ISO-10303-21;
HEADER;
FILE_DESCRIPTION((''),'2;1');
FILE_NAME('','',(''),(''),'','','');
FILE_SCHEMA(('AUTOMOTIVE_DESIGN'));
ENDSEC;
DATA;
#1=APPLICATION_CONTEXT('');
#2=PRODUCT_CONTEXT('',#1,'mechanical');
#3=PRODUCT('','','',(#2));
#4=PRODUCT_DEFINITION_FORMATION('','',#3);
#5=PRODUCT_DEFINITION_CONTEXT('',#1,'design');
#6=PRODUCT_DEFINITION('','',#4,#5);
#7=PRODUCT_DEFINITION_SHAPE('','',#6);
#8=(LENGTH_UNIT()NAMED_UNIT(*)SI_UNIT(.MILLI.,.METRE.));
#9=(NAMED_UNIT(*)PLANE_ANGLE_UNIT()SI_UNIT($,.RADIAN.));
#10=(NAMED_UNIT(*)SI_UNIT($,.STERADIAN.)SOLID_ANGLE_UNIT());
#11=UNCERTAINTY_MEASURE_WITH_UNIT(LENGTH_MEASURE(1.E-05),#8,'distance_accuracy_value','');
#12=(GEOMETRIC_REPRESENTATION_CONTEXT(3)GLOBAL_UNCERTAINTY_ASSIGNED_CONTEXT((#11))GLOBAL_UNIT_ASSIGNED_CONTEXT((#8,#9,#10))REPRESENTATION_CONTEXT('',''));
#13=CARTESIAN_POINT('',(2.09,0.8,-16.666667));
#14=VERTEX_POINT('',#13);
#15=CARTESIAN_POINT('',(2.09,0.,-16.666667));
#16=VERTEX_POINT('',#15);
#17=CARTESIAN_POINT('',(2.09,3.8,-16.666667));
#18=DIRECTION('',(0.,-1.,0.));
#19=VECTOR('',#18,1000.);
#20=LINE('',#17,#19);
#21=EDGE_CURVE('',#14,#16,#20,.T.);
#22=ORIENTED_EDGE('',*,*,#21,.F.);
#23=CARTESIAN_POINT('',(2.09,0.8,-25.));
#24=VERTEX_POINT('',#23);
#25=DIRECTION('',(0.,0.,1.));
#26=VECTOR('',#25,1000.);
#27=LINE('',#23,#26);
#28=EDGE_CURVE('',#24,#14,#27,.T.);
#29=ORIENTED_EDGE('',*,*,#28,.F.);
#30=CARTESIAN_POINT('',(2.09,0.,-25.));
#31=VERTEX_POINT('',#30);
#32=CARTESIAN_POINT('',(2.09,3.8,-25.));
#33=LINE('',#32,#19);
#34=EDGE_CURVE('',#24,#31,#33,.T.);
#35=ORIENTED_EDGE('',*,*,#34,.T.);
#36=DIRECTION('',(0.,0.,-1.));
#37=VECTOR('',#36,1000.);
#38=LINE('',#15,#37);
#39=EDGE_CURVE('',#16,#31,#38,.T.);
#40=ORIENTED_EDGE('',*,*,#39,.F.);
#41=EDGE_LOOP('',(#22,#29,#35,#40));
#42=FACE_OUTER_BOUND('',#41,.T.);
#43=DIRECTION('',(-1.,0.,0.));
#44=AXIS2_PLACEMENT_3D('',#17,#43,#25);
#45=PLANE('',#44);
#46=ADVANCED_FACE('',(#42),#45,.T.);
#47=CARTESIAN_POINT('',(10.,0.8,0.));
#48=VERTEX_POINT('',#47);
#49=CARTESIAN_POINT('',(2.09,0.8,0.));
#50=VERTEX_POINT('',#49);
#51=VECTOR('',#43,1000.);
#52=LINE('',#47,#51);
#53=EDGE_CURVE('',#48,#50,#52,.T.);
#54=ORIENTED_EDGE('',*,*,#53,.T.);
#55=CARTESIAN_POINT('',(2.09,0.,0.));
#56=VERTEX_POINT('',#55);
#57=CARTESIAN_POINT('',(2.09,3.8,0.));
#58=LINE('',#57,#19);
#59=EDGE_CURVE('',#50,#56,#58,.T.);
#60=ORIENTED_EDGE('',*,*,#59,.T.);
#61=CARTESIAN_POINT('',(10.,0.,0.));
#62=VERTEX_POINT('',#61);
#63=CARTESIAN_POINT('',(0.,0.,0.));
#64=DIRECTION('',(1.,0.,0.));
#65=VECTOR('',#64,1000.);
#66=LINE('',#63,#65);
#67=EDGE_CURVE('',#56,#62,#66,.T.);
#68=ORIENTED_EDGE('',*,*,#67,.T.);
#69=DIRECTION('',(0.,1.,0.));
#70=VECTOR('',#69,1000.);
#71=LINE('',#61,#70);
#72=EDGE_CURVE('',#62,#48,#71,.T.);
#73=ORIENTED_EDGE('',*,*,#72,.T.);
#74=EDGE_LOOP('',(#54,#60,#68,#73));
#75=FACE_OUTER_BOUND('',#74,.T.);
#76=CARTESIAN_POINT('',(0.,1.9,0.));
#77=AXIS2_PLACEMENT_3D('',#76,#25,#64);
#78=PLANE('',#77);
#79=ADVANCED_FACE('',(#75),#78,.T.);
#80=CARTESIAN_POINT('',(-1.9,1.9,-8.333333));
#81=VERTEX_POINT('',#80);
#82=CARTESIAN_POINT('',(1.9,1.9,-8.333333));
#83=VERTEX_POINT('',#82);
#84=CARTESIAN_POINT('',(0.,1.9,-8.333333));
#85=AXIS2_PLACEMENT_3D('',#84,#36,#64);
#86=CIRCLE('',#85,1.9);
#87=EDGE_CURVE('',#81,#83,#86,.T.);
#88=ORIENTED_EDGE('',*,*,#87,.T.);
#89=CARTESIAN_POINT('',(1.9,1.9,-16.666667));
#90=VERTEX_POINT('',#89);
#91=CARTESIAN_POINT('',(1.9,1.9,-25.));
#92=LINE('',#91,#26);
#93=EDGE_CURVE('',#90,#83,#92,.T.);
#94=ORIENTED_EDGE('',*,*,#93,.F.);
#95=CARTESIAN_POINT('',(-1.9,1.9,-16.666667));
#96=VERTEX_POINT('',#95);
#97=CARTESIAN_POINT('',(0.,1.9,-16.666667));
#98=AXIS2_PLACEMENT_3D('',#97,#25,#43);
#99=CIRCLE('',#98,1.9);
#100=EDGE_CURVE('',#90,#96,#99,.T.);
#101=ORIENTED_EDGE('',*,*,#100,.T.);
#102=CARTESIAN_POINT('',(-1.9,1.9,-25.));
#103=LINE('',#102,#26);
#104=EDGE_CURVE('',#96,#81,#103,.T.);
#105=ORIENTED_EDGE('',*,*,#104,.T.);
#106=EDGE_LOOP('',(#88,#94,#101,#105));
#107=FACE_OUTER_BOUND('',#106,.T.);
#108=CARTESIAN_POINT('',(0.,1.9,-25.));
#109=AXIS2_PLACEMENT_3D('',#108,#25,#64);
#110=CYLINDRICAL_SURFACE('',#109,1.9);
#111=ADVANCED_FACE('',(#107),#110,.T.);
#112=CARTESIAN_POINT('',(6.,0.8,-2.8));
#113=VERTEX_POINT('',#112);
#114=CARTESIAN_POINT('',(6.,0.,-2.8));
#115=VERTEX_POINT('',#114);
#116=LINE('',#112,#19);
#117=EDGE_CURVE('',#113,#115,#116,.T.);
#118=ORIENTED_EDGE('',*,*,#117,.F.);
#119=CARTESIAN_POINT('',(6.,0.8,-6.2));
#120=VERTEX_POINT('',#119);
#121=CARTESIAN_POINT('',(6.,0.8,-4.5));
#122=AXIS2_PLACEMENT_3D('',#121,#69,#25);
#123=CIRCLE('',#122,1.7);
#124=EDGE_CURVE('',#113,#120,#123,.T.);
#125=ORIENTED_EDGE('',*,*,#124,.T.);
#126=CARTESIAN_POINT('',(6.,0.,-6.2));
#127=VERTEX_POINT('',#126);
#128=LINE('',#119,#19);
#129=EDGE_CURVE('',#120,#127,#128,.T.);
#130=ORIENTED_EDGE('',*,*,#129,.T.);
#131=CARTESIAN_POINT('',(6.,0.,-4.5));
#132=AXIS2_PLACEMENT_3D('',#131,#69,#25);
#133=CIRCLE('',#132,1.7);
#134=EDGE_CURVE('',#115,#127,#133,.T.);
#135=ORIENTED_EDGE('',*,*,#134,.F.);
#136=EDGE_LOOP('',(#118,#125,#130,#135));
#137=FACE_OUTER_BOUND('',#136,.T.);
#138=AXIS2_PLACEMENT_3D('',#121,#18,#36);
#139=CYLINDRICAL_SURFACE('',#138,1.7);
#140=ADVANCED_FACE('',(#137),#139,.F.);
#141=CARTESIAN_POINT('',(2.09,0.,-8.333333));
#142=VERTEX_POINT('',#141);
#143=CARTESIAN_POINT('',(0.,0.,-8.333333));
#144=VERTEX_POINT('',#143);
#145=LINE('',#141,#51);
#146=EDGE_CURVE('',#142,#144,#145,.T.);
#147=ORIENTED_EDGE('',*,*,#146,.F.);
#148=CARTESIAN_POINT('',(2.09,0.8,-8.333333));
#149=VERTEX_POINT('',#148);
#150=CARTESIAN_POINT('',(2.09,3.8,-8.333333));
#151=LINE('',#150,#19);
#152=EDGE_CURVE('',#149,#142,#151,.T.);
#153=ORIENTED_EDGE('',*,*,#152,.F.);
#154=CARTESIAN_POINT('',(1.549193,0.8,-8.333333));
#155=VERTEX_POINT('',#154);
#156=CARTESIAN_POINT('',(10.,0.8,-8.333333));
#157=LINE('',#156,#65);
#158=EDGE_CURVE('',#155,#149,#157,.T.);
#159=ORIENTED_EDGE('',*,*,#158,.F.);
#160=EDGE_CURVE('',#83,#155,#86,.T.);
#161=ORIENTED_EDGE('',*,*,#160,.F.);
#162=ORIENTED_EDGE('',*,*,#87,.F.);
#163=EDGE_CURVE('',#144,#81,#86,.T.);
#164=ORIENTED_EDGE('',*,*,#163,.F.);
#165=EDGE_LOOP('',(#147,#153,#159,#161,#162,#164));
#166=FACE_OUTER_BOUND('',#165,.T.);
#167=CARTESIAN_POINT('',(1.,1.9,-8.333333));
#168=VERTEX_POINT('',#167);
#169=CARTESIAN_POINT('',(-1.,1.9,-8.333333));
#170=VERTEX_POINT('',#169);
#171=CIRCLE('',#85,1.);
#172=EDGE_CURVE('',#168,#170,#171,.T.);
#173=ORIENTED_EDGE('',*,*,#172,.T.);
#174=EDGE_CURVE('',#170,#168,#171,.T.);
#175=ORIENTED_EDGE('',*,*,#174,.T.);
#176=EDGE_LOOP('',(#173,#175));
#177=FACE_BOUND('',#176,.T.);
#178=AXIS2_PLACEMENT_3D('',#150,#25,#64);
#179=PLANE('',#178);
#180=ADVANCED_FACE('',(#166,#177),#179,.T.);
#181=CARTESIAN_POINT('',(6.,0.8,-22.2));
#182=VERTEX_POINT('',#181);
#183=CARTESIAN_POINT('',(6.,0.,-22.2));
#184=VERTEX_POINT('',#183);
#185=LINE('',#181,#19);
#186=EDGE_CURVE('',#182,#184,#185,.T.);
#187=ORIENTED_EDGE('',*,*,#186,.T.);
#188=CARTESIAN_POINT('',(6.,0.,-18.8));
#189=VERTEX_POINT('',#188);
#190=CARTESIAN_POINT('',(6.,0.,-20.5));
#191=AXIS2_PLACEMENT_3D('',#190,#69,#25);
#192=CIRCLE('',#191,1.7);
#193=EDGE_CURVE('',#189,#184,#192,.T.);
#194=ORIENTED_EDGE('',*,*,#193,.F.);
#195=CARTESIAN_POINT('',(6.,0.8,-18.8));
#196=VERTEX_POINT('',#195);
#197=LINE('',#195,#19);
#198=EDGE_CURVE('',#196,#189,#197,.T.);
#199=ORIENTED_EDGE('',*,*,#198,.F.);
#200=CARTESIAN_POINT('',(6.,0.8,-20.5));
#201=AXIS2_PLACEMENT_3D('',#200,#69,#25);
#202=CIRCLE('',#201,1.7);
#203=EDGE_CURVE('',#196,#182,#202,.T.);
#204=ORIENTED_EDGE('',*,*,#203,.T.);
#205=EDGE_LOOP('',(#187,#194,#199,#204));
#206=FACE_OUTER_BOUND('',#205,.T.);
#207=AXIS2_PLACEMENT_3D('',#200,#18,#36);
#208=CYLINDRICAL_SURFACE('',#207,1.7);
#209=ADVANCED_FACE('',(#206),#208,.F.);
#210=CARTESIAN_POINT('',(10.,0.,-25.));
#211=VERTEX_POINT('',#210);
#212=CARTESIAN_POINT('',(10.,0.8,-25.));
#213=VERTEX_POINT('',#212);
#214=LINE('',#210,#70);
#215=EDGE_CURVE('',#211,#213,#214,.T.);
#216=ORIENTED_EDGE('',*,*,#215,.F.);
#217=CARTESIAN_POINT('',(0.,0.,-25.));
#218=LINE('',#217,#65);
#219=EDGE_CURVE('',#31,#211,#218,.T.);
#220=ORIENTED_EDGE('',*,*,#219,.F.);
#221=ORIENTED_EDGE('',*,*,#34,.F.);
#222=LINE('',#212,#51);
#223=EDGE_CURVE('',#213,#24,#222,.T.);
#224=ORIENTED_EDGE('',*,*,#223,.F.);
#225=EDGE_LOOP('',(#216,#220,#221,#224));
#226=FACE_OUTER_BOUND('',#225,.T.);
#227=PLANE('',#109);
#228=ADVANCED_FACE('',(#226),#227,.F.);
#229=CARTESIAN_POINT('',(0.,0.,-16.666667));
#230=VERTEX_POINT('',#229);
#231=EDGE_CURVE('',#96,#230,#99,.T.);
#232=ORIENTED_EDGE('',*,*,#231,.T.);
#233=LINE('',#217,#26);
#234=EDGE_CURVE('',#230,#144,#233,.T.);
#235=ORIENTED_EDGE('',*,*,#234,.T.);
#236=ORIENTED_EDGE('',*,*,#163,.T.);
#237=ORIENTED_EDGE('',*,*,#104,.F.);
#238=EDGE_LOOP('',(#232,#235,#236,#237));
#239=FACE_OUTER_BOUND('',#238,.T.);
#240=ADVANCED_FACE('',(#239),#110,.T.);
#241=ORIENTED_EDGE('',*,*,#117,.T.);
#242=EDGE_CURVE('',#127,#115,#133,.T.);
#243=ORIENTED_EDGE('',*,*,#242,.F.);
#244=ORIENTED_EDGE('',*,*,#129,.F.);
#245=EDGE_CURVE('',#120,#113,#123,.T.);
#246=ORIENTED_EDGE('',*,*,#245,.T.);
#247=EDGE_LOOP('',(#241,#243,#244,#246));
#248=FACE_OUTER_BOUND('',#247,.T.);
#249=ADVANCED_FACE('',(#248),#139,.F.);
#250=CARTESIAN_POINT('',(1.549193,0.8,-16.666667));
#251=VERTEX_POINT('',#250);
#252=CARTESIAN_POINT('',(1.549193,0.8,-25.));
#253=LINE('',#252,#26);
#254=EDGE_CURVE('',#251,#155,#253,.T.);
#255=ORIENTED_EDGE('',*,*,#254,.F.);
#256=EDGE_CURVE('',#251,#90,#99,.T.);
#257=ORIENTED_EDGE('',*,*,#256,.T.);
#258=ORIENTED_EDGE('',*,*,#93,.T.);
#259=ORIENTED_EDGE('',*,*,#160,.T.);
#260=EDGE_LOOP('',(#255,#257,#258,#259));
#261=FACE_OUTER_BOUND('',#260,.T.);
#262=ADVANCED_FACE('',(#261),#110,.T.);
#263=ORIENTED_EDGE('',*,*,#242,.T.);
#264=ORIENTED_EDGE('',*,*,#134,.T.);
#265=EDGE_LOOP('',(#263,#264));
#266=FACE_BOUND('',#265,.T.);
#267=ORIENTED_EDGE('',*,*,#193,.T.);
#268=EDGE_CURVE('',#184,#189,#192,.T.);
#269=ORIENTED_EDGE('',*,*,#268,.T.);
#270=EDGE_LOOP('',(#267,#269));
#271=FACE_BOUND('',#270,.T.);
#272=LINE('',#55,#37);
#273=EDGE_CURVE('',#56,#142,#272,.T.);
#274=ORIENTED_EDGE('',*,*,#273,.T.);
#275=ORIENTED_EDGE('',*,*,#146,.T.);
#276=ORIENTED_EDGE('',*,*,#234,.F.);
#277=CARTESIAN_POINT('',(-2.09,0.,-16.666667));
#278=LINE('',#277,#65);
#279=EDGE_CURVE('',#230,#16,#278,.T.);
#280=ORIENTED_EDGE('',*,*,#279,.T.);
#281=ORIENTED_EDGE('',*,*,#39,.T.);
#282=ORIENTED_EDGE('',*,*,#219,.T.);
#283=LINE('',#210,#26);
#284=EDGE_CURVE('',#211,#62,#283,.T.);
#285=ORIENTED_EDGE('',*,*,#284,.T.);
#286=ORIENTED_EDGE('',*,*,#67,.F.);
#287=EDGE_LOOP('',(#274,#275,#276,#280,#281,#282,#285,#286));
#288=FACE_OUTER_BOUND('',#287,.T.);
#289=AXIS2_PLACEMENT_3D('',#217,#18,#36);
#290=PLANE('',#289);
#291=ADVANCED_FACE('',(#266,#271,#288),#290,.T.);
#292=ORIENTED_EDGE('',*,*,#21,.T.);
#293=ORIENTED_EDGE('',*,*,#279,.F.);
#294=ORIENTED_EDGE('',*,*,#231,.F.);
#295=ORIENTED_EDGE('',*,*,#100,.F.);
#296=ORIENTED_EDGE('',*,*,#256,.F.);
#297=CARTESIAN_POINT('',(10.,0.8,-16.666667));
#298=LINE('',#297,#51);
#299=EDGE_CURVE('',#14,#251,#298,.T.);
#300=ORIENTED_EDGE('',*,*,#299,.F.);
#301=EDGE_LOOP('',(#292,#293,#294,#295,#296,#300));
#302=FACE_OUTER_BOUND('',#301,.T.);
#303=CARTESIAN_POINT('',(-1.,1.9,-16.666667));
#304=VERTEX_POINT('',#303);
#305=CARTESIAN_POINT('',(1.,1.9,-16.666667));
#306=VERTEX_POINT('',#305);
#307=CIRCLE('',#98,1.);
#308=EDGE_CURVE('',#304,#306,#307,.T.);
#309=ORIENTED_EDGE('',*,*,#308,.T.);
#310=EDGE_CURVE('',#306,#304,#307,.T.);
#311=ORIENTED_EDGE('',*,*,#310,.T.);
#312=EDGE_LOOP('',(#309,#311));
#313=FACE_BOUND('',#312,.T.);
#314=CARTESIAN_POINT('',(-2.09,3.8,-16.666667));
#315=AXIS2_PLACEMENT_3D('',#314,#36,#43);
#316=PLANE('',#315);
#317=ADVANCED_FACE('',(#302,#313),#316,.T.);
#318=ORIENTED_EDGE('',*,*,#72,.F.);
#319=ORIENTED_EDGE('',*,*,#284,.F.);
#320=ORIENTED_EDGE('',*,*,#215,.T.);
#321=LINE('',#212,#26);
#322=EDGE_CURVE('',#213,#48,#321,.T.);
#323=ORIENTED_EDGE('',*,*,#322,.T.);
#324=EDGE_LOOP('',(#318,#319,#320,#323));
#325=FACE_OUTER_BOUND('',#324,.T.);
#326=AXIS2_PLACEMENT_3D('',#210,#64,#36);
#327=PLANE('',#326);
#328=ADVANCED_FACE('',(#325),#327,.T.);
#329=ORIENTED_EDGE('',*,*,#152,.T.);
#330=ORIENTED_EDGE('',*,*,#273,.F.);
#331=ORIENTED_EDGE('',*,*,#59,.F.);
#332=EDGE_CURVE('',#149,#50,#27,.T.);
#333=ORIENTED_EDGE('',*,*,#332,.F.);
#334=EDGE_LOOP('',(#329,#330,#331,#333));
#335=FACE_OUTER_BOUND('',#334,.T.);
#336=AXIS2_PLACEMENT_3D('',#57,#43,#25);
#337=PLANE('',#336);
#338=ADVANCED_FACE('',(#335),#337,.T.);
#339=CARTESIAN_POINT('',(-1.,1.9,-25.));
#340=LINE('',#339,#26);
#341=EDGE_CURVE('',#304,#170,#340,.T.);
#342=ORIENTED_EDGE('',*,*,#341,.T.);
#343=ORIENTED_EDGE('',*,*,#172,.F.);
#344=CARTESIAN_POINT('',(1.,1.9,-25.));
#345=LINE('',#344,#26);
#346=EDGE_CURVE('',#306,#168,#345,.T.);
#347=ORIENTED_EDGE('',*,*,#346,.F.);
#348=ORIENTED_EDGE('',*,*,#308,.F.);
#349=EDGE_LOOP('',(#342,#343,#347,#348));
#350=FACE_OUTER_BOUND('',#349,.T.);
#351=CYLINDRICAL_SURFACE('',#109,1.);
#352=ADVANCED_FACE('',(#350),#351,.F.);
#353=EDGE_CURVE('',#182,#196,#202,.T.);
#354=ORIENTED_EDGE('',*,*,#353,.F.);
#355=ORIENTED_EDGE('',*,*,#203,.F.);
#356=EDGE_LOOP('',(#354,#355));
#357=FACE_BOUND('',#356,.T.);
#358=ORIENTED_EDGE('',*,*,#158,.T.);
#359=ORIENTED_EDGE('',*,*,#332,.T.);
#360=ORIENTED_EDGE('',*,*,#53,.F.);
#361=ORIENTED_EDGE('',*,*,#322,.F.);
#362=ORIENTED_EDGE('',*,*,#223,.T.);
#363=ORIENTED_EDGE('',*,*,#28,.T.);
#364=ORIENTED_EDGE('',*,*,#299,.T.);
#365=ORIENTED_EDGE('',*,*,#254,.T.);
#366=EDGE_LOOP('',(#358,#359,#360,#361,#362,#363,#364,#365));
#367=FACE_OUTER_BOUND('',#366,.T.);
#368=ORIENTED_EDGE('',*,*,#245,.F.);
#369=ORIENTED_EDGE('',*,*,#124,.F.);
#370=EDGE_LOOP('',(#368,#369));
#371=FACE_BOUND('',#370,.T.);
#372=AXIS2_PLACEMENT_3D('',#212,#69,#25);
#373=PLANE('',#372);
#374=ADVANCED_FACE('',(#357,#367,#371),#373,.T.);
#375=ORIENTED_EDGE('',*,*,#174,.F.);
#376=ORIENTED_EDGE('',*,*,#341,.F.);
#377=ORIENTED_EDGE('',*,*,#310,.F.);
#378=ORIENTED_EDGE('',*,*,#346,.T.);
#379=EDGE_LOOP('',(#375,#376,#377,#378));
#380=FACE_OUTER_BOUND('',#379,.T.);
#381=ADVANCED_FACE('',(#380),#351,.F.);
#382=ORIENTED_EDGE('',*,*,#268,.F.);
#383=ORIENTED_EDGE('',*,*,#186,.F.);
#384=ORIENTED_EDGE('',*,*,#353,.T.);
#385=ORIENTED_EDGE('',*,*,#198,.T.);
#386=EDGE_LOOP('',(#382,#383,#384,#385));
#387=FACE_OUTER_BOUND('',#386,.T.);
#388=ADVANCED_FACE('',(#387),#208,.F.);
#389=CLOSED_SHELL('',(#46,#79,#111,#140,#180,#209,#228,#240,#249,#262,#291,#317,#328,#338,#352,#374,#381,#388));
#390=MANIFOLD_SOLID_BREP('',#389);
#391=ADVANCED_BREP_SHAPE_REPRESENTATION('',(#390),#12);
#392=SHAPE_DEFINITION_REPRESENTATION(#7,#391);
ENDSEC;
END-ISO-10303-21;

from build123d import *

# Parameters (mm, degrees)
SKETCH_1_R          = 1
EXTRUDE_1_DEPTH     = 25
CUT_EXTRUDE_1_DEPTH = 3.8
SKETCH_3_R          = 1.7
CUT_EXTRUDE_2_DEPTH = 0.8
SKETCH_4_R          = 1.7
CUT_EXTRUDE_3_DEPTH = 0.8


with BuildPart() as part:
    # 草图1 → 凸台-拉伸1 (new body)
    with BuildSketch(Plane.XY):
        with BuildLine():
            Line((0, 0), (10, 0))
            Line((10, 0), (10, 0.8))
            Line((10, 0.8), (1.549193338, 0.8))
            ThreePointArc((1.549193338, 0.8), (-0.871779789, 3.588194302), (0, 0))
        make_face()
        with Locations((0, 1.9)):
            Circle(SKETCH_1_R, mode=Mode.SUBTRACT)
    extrude(amount=-EXTRUDE_1_DEPTH)

    # 草图2 → 切除-拉伸1 (cut)
    with BuildSketch(Plane(origin=(0, 0, 0), x_dir=(1, 0, 0), z_dir=(0, 1, 0))):
        Polygon((-6, 0), (2.09, 0), (2.09, 8.333333333), (-2.09, 8.333333333), (-2.09, 16.666666667), (2.09, 16.666666667), (2.09, 25), (-6, 25), align=None)
    extrude(amount=CUT_EXTRUDE_1_DEPTH, mode=Mode.SUBTRACT)

    # 草图3 → 切除-拉伸2 (cut)
    with BuildSketch(Plane(origin=(0, 0, 0), x_dir=(1, 0, 0), z_dir=(0, 1, 0))):
        with Locations(Location((6, 20.5, 0), (0, 0, 270))):
            Circle(SKETCH_3_R)
    extrude(amount=CUT_EXTRUDE_2_DEPTH, mode=Mode.SUBTRACT)

    # 草图4 → 切除-拉伸3 (cut)
    with BuildSketch(Plane(origin=(0, 0, 0), x_dir=(1, 0, 0), z_dir=(0, 1, 0))):
        with Locations(Location((6, 4.5, 0), (0, 0, 270))):
            Circle(SKETCH_4_R)
    extrude(amount=CUT_EXTRUDE_3_DEPTH, mode=Mode.SUBTRACT)


solid = part.part
